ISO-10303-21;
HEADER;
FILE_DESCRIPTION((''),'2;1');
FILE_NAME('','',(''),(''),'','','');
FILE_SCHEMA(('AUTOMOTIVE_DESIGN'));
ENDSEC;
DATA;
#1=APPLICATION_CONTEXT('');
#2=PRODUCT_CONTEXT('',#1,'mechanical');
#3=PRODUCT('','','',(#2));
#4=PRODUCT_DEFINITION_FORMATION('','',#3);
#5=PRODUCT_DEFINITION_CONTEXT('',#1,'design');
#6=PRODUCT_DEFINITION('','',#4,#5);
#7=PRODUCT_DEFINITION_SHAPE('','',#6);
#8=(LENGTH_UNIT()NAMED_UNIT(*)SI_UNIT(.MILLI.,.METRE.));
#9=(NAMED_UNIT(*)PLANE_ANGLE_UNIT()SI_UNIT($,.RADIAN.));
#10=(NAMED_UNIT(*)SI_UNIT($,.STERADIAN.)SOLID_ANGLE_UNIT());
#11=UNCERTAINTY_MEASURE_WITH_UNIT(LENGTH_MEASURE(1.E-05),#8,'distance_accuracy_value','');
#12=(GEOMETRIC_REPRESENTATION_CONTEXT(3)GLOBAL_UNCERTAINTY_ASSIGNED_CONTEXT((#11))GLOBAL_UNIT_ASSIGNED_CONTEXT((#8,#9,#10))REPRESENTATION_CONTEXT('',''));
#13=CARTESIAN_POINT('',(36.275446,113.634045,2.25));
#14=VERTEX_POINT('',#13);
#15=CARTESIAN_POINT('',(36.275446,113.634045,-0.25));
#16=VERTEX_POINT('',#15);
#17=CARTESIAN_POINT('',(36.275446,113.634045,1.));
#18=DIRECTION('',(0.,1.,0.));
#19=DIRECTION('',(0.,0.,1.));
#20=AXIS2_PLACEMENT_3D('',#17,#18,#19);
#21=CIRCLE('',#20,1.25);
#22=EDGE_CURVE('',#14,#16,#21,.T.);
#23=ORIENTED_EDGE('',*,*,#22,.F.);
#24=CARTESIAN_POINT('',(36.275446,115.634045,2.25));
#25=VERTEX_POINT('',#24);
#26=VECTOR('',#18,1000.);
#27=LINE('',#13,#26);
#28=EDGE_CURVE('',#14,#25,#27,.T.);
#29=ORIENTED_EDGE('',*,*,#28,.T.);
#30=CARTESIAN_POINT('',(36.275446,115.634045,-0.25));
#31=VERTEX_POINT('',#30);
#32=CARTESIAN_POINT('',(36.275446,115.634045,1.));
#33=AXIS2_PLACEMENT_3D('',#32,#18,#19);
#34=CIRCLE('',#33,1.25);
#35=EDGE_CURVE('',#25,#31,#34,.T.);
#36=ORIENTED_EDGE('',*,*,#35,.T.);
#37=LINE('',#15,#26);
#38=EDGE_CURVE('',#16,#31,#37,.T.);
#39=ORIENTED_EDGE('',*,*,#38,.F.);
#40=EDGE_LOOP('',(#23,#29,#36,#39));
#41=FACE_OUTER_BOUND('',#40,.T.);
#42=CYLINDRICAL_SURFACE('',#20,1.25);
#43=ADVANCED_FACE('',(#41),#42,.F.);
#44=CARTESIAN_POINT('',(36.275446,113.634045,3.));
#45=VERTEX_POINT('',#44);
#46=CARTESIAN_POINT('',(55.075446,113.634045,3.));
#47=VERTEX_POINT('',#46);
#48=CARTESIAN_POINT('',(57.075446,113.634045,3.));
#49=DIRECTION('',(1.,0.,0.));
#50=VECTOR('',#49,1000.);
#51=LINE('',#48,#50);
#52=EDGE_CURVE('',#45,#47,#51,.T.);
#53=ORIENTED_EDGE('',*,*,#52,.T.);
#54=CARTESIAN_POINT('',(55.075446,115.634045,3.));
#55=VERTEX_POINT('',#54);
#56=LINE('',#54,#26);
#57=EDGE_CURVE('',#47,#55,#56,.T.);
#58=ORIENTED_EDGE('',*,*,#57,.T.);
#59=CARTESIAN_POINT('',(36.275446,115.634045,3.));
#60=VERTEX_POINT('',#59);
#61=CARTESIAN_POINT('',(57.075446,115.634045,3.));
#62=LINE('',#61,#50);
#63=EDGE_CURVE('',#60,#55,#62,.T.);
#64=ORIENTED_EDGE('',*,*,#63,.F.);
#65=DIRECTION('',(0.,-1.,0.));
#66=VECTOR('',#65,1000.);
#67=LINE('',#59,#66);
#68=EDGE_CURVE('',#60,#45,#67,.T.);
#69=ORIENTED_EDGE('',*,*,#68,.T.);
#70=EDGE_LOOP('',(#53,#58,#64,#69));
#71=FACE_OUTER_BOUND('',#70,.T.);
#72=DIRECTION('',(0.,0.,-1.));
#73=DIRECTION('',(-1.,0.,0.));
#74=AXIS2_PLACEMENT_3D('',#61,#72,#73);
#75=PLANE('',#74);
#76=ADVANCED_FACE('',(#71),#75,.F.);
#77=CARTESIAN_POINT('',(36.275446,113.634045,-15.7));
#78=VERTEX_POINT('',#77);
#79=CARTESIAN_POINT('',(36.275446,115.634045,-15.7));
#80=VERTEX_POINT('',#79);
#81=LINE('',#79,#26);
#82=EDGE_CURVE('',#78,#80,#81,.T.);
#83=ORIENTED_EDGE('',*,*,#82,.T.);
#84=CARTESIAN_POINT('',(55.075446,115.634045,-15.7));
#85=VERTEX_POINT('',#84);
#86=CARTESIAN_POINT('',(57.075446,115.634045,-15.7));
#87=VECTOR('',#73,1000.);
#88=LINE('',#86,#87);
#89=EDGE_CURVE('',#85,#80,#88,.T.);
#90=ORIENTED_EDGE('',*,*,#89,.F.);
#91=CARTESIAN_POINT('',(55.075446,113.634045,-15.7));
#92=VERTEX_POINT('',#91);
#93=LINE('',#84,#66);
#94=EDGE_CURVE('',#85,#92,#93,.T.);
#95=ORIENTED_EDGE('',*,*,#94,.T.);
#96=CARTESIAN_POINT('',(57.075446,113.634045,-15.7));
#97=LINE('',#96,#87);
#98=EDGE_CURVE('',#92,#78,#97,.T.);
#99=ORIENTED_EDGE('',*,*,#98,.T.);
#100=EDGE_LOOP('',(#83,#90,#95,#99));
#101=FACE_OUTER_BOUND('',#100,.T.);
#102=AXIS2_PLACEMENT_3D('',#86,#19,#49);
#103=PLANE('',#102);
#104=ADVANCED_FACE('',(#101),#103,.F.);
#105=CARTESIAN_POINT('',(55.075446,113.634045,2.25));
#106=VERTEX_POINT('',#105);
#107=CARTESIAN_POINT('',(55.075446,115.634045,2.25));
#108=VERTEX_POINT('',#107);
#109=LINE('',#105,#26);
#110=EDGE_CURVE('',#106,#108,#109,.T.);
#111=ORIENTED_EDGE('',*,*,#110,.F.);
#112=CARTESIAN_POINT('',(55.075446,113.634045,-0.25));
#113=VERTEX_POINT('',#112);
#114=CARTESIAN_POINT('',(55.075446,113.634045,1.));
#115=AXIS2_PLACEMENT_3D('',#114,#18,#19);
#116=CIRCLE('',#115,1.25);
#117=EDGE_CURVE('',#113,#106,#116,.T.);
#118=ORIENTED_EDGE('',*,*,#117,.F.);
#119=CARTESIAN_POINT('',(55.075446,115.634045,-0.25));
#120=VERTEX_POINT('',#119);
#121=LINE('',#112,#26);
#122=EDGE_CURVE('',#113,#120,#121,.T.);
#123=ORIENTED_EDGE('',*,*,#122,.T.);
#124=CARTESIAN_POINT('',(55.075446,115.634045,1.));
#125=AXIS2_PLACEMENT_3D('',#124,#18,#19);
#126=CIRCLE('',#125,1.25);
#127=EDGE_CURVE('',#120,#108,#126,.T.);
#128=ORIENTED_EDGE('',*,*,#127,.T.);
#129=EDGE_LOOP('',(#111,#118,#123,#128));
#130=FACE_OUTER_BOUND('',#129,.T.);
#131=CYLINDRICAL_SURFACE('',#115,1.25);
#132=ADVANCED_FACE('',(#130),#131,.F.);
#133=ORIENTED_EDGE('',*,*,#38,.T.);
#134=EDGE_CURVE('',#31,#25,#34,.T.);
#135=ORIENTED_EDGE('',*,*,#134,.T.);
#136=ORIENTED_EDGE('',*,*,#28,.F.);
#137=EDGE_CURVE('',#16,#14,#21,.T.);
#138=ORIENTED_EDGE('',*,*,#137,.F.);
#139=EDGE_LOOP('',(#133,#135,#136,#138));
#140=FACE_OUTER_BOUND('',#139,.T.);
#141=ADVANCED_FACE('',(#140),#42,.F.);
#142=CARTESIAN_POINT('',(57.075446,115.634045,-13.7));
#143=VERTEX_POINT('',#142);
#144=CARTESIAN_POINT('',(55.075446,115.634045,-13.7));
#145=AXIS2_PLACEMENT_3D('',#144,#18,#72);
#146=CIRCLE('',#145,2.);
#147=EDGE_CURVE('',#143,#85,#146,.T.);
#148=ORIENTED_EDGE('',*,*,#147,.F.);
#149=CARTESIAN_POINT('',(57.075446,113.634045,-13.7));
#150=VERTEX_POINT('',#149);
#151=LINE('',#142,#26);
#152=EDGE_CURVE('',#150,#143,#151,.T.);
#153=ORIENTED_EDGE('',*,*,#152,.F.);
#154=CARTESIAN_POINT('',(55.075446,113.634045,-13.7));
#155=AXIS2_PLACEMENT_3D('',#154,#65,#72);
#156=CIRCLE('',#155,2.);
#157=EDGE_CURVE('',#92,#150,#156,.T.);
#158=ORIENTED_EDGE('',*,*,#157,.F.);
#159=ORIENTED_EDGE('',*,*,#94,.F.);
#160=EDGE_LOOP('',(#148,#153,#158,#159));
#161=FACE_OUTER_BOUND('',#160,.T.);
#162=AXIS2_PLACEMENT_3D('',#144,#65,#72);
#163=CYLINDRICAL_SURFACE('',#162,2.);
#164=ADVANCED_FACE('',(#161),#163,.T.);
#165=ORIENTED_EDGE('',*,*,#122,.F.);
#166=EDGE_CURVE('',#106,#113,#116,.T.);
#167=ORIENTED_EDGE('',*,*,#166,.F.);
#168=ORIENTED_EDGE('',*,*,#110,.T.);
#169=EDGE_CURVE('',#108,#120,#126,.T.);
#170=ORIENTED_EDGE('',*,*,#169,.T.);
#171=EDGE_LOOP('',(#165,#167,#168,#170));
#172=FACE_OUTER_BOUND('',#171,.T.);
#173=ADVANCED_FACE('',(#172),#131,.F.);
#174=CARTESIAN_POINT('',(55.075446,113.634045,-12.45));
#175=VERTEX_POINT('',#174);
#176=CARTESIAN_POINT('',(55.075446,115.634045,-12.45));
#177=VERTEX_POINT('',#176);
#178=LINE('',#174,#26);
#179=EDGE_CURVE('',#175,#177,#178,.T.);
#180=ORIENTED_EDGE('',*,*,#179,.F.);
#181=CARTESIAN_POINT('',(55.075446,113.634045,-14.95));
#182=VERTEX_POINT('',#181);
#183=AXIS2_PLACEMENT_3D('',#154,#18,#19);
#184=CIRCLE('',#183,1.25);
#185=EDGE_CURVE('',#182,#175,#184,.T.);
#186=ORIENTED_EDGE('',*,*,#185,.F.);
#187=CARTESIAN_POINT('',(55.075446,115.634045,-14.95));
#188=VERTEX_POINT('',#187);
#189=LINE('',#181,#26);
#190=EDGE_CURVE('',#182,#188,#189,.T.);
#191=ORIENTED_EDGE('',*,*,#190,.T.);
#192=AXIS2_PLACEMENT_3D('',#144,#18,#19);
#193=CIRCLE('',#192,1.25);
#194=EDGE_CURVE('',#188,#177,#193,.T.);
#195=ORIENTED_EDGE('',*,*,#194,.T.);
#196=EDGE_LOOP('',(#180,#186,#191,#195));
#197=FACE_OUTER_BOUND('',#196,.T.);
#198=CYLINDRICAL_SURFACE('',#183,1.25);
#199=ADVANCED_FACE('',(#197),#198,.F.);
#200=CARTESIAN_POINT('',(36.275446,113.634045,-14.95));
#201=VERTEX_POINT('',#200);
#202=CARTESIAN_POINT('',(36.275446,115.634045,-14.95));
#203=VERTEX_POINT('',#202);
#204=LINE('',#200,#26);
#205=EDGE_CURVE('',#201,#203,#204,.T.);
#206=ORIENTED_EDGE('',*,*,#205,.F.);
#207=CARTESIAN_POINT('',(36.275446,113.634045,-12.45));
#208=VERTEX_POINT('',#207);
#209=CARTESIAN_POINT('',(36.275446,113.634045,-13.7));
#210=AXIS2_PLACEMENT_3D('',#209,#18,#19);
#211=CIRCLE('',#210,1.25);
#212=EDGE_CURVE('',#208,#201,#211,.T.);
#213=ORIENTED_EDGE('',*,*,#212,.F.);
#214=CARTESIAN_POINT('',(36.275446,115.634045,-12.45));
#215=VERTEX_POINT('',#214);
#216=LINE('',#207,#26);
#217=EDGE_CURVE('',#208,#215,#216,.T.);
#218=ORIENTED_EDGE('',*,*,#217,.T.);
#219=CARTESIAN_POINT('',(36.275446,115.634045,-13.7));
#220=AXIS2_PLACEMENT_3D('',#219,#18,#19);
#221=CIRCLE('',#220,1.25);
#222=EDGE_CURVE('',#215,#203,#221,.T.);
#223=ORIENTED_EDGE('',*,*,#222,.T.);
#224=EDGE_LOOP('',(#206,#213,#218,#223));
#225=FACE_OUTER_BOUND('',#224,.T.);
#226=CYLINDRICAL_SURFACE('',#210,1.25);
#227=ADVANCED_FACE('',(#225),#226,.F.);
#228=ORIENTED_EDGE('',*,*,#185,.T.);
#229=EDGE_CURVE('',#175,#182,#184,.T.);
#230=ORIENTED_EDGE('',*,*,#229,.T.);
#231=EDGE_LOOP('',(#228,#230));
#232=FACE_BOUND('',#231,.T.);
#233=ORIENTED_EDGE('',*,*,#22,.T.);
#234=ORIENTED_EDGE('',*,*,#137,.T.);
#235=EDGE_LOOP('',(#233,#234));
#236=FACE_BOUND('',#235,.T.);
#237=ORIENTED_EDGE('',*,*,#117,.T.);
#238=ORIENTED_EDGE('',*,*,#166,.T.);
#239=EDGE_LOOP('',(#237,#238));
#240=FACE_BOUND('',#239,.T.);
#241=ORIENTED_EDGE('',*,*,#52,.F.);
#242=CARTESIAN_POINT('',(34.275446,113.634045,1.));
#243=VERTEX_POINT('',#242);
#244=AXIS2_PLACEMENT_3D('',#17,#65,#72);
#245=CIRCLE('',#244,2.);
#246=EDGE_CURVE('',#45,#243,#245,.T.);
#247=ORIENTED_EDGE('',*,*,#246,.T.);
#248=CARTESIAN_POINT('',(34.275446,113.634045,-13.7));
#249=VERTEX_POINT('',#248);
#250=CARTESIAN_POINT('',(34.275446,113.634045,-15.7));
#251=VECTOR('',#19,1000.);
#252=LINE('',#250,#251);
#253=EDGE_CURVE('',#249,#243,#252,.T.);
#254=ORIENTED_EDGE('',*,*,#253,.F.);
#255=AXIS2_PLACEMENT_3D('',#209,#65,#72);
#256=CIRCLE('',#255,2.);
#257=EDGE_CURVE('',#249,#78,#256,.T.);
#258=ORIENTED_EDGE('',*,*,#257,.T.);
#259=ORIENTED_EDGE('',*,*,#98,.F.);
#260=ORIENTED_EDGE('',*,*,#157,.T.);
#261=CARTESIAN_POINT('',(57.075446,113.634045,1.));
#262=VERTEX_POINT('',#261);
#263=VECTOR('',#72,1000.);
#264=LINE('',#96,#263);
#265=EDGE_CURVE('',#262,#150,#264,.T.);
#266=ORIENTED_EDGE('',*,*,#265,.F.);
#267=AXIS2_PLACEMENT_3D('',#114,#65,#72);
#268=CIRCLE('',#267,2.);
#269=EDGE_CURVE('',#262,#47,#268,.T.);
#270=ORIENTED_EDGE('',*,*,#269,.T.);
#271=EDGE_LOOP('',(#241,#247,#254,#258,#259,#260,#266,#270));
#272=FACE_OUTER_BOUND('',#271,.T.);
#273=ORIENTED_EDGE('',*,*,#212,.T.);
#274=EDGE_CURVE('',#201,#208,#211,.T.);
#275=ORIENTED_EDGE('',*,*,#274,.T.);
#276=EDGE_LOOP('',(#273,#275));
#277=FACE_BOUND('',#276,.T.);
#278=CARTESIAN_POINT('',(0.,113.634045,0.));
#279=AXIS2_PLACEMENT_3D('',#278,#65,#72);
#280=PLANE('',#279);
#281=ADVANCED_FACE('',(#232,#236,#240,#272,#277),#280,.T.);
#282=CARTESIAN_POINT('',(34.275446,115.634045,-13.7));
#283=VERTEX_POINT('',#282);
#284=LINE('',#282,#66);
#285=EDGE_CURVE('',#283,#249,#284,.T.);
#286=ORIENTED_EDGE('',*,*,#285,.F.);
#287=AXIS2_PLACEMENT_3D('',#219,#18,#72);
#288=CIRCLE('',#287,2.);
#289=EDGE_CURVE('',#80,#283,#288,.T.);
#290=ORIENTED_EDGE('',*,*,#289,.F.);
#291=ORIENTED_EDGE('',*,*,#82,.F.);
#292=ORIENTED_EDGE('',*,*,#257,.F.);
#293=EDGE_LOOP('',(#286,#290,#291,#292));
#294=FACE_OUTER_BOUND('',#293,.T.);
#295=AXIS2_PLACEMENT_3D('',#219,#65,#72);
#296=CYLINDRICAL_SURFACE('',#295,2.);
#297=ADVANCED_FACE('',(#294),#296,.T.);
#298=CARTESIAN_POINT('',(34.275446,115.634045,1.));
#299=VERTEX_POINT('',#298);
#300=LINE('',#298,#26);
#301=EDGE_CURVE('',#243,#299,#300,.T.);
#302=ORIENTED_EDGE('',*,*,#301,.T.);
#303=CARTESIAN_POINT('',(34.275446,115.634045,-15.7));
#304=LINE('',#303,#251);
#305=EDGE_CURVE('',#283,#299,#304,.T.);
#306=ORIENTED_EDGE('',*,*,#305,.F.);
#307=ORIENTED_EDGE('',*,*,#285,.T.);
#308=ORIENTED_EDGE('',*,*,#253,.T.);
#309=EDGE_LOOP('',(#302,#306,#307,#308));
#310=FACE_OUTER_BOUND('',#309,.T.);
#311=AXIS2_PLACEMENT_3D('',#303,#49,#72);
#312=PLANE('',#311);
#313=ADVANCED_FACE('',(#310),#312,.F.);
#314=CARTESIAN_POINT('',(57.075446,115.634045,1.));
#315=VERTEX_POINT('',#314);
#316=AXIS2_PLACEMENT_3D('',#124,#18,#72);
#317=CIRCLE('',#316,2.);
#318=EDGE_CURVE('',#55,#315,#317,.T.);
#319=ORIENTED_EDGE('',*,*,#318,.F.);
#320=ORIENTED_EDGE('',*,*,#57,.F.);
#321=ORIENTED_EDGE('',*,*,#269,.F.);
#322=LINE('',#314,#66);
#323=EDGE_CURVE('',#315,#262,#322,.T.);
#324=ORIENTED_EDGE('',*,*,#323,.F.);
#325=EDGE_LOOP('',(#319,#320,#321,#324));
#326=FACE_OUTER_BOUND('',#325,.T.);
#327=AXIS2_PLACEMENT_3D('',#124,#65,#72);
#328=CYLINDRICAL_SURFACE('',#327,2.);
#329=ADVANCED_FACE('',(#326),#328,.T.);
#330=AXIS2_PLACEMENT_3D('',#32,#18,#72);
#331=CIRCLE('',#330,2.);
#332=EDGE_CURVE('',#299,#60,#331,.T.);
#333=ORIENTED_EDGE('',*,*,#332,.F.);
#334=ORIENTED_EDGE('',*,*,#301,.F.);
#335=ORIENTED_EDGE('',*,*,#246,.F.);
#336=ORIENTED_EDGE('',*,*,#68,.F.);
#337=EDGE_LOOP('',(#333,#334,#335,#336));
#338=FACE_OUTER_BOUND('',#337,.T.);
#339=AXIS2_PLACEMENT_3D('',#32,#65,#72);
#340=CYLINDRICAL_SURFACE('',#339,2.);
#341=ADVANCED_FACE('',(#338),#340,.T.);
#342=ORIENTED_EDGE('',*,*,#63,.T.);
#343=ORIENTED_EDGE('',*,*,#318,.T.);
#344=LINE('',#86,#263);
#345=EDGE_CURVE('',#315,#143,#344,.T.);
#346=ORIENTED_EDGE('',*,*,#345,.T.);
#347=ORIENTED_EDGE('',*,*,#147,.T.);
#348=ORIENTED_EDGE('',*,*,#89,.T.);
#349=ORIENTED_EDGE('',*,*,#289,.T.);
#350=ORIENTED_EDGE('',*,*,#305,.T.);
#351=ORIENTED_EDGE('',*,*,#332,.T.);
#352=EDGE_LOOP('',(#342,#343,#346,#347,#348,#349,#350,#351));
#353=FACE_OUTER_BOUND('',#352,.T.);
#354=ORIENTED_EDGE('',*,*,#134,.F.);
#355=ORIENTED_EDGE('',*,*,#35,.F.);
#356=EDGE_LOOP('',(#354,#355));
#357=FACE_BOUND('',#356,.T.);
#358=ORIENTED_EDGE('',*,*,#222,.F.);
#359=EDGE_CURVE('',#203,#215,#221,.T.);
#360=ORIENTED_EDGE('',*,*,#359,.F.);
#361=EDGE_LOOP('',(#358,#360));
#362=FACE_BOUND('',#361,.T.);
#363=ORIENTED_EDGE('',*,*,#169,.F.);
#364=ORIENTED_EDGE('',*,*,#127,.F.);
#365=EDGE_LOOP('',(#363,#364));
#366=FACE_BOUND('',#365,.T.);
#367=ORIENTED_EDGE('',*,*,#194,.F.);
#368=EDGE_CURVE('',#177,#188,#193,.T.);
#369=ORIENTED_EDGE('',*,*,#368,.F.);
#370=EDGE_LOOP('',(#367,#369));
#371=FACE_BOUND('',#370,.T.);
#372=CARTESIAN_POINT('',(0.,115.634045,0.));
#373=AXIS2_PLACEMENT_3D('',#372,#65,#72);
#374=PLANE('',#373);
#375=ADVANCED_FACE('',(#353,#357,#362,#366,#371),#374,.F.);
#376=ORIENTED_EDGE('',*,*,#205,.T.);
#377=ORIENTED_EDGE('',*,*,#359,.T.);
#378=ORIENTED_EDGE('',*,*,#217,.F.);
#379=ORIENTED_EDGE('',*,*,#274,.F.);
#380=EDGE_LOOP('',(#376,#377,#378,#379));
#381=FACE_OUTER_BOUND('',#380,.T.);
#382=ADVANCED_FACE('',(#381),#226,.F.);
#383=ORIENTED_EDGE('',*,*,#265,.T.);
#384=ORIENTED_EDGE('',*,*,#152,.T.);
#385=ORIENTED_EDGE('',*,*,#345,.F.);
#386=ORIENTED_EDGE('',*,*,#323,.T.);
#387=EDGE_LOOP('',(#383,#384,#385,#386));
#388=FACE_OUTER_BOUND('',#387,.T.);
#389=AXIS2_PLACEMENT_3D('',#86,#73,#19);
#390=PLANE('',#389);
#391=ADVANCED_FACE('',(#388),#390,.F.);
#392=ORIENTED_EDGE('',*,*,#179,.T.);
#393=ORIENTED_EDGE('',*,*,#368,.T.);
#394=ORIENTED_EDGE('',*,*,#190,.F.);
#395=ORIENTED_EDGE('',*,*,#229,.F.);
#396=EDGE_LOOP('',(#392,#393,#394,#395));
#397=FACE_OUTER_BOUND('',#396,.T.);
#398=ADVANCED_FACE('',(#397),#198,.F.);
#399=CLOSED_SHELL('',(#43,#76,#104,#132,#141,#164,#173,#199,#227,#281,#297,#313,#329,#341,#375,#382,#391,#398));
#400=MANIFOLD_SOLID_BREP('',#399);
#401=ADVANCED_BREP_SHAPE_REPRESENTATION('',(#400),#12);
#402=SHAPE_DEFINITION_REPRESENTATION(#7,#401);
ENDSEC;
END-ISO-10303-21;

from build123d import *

# Parameters (mm, degrees)
EXTRUDE_THIN1_DEPTH     = 12.7
SKETCH3_W               = 22.8
SKETCH3_H               = 18.7
BOSS_EXTRUDE2_DEPTH     = 2
FILLET1_R               = 2
SKETCH4_R               = 1.25
CUT_EXTRUDE1_DEPTH      = 2
CUT_EXTRUDE2_DEPTH      = 61.42253709
CUT_EXTRUDE2_DEPTH_BACK = 61.42253709
SKETCH5_R               = 2.75
SKETCH6_R               = 1.25
CUT_EXTRUDE3_DEPTH      = 10
CUT_EXTRUDE4_DEPTH      = 131.301684531
CUT_EXTRUDE4_DEPTH_BACK = 131.301684531
SKETCH7_W               = 21.210036283
SKETCH7_H               = 32.49756926


with BuildPart() as part:
    # Sketch1 → Extrude-Thin1 (new body)
    with BuildSketch(Plane.XY):
        Polygon((51.165574182, 84.975681723), (42.185318061, 93.955937844), (42.185318061, 113.634045339), (40.185318061, 113.634045339), (40.185318061, 93.127510719), (49.75136062, 83.561468161), align=None)
    extrude(amount=-EXTRUDE_THIN1_DEPTH)

    # Sketch5 → Cut-Extrude2 (cut, two sides: drawn at the far end of the back side and taken through both)
    with BuildSketch(Plane(origin=(68.070627953, 68.070627953, 0), x_dir=(0, 0, -1), z_dir=(0.7071067811865513, 0.7071067811865437, 0)).offset(-CUT_EXTRUDE2_DEPTH_BACK)):
        with Locations(Location((6.35, 30.257356315, 0), (0, 0, 90))):
            Circle(SKETCH5_R)
    extrude(amount=CUT_EXTRUDE2_DEPTH + CUT_EXTRUDE2_DEPTH_BACK, mode=Mode.SUBTRACT)

    # Sketch6 → Cut-Extrude3 (cut)
    with BuildSketch(Plane(origin=(66.65641439, 66.65641439, 0), x_dir=(0, 0, 1), z_dir=(-0.7071067811865513, -0.7071067811865437, 0))):
        with Locations(Location((-10.65, 34.557356315, 0), (0, 0, 270))):
            Circle(SKETCH6_R)
        with Locations(Location((-2.05, 34.557356315, 0), (0, 0, 270))):
            Circle(SKETCH6_R)
        with Locations(Location((-2.05, 25.957356315, 0), (0, 0, 270))):
            Circle(SKETCH6_R)
        with Locations(Location((-10.65, 25.957356315, 0), (0, 0, 270))):
            Circle(SKETCH6_R)
    extrude(amount=-CUT_EXTRUDE3_DEPTH, mode=Mode.SUBTRACT)

    # Sketch7 → Cut-Extrude4 (cut, two sides: drawn at the far end of the back side and taken through both)
    with BuildSketch(Plane.XY.offset(3).offset(-CUT_EXTRUDE4_DEPTH_BACK)):
        with Locations((44.470427981, 97.385260709)):
            Rectangle(SKETCH7_W, SKETCH7_H)
    extrude(amount=CUT_EXTRUDE4_DEPTH + CUT_EXTRUDE4_DEPTH_BACK, mode=Mode.SUBTRACT)


with BuildPart() as body_2:
    # Sketch3 → Boss-Extrude2 (new body)
    with BuildSketch(Plane(origin=(0, 113.634045339, 0), x_dir=(1, 0, 0), z_dir=(0, 1, 0))):
        with Locations((45.675446122, 6.35)):
            Rectangle(SKETCH3_W, SKETCH3_H)
    extrude(amount=BOSS_EXTRUDE2_DEPTH)

    # Fillet1
    fillet1_edges = [body_2.edges().sort_by_distance(p)[0] for p in [
        (57.075446122, 114.634045339, 3),
        (34.275446122, 114.634045339, 3),
        (34.275446122, 114.634045339, -15.7),
        (57.075446122, 114.634045339, -15.7),
    ]]
    fillet(fillet1_edges, radius=FILLET1_R)

    # Sketch4 → Cut-Extrude1 (cut)
    with BuildSketch(Plane(origin=(0, 115.634045339, 0), x_dir=(1, 0, 0), z_dir=(0, 1, 0))):
        with Locations(Location((55.075446122, 13.7, 0), (0, 0, 270))):
            Circle(SKETCH4_R)
        with Locations(Location((55.075446122, -1, 0), (0, 0, 270))):
            Circle(SKETCH4_R)
        with Locations(Location((36.275446122, -1, 0), (0, 0, 270))):
            Circle(SKETCH4_R)
        with Locations(Location((36.275446122, 13.7, 0), (0, 0, 270))):
            Circle(SKETCH4_R)
    extrude(amount=-CUT_EXTRUDE1_DEPTH, mode=Mode.SUBTRACT)


solid = body_2.part
